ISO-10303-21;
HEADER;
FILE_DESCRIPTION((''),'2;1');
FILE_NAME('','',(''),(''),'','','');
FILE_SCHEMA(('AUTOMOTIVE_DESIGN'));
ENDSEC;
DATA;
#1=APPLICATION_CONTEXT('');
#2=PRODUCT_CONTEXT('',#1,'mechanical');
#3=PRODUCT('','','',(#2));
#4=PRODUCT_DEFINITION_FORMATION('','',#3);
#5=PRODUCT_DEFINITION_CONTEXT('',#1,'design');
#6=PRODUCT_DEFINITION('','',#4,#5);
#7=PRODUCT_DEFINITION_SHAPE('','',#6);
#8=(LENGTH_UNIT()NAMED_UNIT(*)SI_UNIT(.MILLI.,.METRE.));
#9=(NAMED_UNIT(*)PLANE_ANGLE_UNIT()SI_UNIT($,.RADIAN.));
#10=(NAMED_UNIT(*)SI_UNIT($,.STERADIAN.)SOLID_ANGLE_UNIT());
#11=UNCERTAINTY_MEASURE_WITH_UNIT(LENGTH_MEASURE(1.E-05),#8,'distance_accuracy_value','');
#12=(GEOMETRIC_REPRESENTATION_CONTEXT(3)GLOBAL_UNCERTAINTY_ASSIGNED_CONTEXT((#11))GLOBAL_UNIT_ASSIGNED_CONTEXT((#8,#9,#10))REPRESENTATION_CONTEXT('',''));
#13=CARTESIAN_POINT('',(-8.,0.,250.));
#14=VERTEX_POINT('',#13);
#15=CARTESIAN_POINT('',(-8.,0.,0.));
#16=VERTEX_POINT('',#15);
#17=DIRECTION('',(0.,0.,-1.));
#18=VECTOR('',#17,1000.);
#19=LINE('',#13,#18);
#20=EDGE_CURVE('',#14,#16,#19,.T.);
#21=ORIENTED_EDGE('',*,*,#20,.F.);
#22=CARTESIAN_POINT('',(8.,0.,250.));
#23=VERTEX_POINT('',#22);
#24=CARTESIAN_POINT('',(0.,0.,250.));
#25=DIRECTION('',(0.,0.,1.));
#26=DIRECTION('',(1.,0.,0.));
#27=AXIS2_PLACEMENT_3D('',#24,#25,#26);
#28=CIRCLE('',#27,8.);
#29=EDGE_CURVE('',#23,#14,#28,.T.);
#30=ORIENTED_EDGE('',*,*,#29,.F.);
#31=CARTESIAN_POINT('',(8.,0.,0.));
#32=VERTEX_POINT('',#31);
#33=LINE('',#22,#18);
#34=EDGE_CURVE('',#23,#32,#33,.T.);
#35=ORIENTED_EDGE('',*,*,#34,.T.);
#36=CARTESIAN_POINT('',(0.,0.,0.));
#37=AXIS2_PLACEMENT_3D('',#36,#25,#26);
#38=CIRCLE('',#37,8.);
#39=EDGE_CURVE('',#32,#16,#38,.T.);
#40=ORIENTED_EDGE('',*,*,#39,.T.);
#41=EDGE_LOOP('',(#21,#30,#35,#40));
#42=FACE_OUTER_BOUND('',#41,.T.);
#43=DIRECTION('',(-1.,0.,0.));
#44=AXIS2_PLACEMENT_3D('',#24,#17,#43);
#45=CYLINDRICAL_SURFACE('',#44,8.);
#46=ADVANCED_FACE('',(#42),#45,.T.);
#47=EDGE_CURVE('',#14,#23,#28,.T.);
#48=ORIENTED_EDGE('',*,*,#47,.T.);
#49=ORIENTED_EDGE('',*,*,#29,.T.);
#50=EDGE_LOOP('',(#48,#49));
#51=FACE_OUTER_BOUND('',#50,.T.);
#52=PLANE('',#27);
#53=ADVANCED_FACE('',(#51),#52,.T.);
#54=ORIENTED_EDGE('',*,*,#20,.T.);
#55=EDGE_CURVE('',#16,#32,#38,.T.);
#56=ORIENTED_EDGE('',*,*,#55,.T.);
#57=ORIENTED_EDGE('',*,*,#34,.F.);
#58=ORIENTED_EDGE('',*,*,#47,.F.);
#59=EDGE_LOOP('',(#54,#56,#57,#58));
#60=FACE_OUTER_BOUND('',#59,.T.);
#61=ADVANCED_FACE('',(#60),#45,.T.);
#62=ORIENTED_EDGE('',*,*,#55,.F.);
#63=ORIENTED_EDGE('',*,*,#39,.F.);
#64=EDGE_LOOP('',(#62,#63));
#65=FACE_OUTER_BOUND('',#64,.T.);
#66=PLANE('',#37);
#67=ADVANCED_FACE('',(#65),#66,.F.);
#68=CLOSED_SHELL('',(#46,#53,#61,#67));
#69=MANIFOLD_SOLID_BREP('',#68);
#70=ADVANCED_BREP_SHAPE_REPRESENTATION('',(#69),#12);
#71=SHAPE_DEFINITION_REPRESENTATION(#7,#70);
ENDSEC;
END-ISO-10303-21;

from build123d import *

# Parameters (mm, degrees)
SKETCH_1_R      = 8
EXTRUDE_1_DEPTH = 250


with BuildPart() as part:
    # 草图1 → 凸台-拉伸1 (new body)
    with BuildSketch(Plane.XY):
        Circle(SKETCH_1_R)
    extrude(amount=EXTRUDE_1_DEPTH)


solid = part.part
